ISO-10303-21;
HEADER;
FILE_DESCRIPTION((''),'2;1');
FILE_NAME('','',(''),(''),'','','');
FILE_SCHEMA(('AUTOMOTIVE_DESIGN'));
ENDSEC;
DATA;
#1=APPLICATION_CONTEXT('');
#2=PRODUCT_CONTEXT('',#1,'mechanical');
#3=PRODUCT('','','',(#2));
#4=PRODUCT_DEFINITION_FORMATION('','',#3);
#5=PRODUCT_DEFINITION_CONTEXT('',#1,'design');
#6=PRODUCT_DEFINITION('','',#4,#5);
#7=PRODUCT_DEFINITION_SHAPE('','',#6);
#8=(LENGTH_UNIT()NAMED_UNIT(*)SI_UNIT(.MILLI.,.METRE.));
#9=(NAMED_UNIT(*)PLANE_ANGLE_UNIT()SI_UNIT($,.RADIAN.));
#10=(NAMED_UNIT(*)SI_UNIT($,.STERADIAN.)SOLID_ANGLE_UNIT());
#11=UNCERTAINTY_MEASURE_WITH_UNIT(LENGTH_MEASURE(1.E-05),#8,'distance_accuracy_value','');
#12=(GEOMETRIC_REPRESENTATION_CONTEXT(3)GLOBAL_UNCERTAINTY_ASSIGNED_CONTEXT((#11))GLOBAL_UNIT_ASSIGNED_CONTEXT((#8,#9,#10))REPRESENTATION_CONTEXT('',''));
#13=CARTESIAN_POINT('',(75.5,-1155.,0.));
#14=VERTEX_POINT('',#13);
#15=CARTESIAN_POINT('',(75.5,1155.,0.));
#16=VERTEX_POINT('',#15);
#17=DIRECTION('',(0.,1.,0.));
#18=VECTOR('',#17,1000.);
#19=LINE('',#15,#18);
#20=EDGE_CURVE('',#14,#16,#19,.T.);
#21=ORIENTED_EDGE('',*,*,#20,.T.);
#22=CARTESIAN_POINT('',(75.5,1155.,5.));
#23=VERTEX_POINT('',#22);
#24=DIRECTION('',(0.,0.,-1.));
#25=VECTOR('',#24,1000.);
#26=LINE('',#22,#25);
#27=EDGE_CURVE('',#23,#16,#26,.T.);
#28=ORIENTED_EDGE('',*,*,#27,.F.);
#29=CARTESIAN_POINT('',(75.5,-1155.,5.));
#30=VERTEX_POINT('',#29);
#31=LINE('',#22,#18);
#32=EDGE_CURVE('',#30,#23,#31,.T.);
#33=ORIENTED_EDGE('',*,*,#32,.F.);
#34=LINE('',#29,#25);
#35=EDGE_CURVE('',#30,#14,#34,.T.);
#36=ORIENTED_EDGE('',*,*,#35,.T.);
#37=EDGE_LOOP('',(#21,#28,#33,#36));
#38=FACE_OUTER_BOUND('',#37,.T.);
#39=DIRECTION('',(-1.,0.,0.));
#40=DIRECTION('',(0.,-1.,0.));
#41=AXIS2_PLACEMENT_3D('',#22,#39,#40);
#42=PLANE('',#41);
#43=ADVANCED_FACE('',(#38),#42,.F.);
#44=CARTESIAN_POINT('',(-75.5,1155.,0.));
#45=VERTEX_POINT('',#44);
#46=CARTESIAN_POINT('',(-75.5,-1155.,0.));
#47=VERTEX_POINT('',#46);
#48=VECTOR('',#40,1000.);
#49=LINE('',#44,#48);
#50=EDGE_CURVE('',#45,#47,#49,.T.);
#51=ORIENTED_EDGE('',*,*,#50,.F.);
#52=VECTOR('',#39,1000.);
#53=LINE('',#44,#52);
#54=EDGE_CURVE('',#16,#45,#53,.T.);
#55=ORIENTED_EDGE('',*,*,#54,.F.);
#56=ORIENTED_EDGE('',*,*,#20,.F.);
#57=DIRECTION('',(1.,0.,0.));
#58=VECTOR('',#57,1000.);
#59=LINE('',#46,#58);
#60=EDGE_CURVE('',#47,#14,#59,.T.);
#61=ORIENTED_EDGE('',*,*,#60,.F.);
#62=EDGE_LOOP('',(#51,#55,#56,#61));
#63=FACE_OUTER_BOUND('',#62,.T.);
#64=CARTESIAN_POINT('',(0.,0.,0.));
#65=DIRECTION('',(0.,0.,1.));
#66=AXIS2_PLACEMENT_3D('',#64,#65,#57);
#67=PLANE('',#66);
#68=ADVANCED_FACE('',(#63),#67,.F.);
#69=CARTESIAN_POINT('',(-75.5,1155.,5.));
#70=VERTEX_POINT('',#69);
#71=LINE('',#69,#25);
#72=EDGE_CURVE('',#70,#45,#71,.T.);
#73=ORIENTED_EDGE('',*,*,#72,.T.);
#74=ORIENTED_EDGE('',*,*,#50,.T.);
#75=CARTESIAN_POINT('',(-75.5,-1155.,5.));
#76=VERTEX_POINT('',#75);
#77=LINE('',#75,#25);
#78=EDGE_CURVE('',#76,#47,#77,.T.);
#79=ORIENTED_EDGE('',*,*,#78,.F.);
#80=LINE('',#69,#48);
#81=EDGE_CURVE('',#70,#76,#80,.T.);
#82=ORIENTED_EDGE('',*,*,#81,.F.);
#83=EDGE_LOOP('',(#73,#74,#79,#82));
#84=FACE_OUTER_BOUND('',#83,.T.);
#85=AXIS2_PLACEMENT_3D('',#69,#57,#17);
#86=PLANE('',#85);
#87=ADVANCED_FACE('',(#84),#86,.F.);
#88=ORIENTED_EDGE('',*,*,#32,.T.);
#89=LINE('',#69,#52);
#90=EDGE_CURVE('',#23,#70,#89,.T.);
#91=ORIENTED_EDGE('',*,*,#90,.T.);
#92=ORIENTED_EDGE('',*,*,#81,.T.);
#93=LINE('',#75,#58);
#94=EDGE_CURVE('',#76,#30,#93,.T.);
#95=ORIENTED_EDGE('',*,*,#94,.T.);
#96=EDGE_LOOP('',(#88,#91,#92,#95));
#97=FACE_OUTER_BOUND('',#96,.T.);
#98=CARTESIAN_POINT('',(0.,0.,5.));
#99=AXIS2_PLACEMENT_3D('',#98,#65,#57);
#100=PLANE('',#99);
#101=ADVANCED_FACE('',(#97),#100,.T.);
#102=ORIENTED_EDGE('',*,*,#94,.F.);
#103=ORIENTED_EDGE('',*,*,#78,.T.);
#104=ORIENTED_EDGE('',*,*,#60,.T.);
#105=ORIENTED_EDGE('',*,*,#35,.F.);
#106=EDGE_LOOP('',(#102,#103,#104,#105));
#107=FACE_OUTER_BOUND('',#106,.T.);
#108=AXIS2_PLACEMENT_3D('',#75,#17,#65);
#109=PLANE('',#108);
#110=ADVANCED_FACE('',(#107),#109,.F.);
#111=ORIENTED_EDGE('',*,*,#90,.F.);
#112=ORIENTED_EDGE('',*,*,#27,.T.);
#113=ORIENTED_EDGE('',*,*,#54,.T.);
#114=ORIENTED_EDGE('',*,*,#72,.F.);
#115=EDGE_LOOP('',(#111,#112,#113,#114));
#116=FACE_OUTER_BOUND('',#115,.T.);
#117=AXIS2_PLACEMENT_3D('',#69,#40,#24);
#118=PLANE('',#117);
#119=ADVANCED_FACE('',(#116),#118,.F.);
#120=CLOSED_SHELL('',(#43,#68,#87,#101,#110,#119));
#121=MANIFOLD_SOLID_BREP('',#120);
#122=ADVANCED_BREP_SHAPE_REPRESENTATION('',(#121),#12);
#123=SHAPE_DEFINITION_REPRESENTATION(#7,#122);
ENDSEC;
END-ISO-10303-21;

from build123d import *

# Parameters (mm, degrees)
SKETCH_1_W      = 151
SKETCH_1_H      = 2310
EXTRUDE_1_DEPTH = 5


with BuildPart() as part:
    # 草图1 → 凸台-拉伸1 (new body)
    with BuildSketch(Plane.XY):
        Rectangle(SKETCH_1_W, SKETCH_1_H)
    extrude(amount=EXTRUDE_1_DEPTH)


solid = part.part
